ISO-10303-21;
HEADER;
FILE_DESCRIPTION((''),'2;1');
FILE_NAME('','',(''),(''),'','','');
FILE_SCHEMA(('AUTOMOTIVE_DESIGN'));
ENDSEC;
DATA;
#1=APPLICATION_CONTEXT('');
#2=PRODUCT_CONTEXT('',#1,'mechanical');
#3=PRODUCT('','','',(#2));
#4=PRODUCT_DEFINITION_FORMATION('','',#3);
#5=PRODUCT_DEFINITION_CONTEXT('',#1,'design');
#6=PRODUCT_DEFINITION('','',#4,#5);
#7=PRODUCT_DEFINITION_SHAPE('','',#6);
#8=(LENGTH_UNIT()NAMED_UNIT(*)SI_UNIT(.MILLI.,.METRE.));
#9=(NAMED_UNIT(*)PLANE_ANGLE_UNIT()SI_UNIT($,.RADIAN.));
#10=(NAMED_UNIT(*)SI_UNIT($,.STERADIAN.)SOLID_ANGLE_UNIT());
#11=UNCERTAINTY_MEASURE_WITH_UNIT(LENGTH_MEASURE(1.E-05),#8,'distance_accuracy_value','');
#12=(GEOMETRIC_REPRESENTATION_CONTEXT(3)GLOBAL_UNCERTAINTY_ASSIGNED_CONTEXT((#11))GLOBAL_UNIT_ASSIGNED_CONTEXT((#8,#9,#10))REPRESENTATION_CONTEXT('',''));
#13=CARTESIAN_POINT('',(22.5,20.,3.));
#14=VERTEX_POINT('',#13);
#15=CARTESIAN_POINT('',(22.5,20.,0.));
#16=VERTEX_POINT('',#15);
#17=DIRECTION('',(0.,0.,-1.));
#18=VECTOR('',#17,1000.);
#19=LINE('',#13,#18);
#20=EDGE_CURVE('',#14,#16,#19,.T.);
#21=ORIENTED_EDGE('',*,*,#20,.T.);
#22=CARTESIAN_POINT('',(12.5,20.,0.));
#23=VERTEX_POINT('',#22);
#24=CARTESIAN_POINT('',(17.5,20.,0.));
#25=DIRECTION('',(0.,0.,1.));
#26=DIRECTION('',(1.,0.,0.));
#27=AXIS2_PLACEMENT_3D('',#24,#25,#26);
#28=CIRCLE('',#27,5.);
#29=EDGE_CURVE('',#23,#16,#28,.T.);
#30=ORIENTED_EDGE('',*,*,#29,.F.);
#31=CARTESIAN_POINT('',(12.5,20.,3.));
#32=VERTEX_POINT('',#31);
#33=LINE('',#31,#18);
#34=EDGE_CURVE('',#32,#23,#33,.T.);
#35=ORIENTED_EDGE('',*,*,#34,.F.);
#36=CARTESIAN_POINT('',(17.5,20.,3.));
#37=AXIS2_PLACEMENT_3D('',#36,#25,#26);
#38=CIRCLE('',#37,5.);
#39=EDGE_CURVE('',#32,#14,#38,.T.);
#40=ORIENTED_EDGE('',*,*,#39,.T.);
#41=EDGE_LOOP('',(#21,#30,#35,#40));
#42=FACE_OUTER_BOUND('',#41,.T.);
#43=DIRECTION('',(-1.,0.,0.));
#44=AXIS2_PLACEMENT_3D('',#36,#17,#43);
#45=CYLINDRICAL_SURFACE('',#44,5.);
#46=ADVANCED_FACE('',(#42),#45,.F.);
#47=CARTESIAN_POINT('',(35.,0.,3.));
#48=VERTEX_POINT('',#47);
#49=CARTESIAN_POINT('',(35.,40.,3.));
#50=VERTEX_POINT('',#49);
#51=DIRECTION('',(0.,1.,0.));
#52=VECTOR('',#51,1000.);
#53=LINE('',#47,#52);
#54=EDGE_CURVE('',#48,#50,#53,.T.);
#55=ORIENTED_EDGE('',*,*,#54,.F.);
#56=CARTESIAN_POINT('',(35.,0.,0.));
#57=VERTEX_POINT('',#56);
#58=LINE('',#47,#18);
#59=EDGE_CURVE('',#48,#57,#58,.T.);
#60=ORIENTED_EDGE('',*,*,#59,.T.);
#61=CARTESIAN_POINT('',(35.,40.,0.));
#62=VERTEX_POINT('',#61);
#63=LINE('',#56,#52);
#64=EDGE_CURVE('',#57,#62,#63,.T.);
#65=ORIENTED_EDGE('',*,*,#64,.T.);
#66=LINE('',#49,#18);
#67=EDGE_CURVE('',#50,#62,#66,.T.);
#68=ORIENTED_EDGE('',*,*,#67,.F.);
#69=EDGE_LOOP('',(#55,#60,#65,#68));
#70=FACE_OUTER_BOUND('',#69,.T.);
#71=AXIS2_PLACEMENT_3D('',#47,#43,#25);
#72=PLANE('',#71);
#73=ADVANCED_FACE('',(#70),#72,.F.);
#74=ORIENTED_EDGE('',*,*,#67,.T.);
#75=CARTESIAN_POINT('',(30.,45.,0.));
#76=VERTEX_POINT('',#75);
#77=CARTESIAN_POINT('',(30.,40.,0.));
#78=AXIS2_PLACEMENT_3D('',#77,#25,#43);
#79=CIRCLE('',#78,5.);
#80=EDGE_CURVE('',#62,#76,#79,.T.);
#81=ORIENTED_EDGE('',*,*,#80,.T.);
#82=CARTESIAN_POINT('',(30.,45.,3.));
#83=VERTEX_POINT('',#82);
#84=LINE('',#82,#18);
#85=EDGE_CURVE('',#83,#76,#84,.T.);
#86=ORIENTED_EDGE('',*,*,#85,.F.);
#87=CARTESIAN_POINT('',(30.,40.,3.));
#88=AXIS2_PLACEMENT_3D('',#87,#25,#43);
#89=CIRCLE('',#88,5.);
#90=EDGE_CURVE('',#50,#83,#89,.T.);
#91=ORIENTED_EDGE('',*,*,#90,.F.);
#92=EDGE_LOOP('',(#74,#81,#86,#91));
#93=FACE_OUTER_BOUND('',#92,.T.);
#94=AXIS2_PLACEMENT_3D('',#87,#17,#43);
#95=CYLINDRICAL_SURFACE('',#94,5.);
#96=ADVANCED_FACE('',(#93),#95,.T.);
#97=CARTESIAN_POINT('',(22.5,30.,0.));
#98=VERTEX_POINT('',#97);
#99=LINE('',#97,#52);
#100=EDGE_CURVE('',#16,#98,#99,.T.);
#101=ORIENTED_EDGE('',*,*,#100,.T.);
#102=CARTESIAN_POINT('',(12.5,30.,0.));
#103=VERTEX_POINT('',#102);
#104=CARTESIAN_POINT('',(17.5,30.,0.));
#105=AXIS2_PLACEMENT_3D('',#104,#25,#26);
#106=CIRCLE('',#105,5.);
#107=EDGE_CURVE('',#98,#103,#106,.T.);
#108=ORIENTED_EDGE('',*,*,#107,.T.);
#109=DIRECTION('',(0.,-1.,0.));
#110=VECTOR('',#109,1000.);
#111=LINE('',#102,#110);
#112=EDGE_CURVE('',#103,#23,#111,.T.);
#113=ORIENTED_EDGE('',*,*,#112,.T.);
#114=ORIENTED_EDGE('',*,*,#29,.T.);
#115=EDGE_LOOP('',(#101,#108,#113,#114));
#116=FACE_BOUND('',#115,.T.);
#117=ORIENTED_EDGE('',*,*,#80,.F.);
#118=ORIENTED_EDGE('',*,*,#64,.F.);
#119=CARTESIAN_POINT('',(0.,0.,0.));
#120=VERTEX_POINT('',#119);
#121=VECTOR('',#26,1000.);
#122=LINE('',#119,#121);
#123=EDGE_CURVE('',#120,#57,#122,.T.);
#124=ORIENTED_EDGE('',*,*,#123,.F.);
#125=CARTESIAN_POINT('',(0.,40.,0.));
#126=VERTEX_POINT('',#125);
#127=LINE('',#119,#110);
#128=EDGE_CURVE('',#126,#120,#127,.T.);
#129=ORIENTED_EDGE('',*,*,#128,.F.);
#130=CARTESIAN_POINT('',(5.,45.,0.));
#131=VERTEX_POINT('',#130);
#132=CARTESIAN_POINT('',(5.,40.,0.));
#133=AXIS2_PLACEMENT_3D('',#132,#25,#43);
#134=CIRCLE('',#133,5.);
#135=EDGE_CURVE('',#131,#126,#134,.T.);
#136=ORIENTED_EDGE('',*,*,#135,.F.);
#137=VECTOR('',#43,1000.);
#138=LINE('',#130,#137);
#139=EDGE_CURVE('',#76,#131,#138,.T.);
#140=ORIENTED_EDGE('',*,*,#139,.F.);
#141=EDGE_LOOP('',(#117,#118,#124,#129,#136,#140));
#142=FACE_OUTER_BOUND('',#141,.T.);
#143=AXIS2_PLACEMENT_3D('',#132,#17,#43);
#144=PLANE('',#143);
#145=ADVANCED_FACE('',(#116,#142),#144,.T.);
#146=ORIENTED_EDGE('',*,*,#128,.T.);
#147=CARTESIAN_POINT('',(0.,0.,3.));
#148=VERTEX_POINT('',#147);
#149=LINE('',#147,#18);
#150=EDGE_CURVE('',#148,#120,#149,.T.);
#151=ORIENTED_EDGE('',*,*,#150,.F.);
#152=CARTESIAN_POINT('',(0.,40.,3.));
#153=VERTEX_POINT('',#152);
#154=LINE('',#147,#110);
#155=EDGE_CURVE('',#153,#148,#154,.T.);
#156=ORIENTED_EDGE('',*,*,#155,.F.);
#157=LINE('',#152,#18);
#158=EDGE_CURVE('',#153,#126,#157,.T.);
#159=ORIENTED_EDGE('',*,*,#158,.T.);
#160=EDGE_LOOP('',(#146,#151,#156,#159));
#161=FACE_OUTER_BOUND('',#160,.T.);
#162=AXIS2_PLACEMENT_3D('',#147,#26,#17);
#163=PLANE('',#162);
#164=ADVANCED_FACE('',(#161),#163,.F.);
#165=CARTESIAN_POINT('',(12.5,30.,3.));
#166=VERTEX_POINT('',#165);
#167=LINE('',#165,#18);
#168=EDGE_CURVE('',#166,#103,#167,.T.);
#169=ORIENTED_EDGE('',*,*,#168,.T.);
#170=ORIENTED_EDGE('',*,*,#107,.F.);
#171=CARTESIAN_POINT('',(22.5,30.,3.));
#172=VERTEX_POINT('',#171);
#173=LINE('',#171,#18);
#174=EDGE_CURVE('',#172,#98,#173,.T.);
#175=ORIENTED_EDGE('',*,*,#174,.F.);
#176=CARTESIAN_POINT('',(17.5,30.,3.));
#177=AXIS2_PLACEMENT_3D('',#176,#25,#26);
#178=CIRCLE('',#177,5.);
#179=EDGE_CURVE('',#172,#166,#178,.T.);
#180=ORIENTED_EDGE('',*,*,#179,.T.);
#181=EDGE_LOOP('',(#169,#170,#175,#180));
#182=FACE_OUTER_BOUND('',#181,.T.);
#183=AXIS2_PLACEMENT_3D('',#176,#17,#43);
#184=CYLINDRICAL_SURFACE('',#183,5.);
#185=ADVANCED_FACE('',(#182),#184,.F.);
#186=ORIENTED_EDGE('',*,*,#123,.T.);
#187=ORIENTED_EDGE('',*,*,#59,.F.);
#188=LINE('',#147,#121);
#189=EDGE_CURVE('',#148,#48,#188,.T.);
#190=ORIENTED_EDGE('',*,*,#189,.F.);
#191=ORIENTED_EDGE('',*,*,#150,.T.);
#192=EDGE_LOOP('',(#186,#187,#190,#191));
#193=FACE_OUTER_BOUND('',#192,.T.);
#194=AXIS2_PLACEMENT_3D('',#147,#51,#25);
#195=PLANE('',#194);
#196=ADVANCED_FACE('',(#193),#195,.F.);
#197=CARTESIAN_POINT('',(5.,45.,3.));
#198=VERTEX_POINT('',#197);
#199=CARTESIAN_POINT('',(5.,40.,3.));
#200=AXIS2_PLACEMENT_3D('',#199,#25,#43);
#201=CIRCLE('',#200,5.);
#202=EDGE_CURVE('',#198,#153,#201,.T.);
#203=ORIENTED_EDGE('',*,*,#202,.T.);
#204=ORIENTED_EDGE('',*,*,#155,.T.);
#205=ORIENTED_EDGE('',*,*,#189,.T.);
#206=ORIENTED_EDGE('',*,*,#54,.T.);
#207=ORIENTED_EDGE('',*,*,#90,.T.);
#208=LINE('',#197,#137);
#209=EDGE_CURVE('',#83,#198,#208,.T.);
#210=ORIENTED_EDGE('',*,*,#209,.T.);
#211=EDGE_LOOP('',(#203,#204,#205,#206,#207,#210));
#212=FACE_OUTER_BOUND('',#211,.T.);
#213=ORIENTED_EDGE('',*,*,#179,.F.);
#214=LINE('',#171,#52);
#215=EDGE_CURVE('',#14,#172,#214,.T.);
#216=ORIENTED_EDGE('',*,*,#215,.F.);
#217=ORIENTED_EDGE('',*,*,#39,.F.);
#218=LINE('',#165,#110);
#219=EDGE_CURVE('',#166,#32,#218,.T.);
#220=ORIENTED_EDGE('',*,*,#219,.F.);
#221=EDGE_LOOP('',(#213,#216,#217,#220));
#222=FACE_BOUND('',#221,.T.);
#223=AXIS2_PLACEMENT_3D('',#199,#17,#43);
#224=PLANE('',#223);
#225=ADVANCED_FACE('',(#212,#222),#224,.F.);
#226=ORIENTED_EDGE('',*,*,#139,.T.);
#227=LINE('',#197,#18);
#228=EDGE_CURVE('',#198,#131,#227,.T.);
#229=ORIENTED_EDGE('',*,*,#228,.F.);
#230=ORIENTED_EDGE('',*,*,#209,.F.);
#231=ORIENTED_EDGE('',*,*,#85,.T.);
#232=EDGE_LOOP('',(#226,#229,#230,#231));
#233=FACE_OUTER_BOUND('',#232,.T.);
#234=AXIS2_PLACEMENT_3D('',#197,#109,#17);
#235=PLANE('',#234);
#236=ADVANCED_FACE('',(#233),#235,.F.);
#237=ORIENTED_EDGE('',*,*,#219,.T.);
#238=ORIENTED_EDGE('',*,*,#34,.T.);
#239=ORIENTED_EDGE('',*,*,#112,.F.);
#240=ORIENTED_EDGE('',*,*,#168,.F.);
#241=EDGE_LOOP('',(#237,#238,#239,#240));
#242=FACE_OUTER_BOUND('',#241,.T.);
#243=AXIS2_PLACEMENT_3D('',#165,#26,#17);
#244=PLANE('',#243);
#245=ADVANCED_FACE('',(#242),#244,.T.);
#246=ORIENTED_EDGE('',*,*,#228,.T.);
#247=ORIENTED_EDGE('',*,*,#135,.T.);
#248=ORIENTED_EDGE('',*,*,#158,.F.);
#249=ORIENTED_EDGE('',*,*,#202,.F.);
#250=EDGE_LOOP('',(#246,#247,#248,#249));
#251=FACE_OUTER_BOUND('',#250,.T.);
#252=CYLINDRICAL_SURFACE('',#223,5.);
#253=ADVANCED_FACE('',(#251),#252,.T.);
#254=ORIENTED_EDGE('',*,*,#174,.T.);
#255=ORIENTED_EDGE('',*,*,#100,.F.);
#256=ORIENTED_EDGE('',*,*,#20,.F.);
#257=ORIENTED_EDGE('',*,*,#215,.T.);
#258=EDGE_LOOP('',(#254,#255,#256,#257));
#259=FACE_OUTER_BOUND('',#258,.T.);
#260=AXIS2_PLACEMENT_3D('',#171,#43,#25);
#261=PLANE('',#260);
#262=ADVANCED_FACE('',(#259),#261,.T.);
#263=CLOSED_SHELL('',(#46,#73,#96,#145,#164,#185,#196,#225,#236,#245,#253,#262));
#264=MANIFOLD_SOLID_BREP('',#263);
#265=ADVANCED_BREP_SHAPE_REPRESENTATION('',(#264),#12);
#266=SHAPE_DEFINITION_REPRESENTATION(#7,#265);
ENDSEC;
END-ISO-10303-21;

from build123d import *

# Parameters (mm, degrees)
BOSS_EXTRUDE1_DEPTH = 3


with BuildPart() as part:
    # Sketch1 → Boss-Extrude1 (new body)
    with BuildSketch(Plane.XY):
        with BuildLine():
            Line((0, 0), (35, 0))
            Line((35, 0), (35, 40))
            ThreePointArc((35, 40), (33.535533906, 43.535533906), (30, 45))
            Line((30, 45), (5, 45))
            ThreePointArc((5, 45), (1.464466094, 43.535533906), (0, 40))
            Line((0, 40), (0, 0))
        make_face()
        with BuildLine():
            Line((12.5, 30), (12.5, 20))
            ThreePointArc((12.5, 20), (17.5, 15), (22.5, 20))
            Line((22.5, 20), (22.5, 30))
            ThreePointArc((22.5, 30), (17.5, 35), (12.5, 30))
        make_face(mode=Mode.SUBTRACT)
    extrude(amount=BOSS_EXTRUDE1_DEPTH)


solid = part.part
